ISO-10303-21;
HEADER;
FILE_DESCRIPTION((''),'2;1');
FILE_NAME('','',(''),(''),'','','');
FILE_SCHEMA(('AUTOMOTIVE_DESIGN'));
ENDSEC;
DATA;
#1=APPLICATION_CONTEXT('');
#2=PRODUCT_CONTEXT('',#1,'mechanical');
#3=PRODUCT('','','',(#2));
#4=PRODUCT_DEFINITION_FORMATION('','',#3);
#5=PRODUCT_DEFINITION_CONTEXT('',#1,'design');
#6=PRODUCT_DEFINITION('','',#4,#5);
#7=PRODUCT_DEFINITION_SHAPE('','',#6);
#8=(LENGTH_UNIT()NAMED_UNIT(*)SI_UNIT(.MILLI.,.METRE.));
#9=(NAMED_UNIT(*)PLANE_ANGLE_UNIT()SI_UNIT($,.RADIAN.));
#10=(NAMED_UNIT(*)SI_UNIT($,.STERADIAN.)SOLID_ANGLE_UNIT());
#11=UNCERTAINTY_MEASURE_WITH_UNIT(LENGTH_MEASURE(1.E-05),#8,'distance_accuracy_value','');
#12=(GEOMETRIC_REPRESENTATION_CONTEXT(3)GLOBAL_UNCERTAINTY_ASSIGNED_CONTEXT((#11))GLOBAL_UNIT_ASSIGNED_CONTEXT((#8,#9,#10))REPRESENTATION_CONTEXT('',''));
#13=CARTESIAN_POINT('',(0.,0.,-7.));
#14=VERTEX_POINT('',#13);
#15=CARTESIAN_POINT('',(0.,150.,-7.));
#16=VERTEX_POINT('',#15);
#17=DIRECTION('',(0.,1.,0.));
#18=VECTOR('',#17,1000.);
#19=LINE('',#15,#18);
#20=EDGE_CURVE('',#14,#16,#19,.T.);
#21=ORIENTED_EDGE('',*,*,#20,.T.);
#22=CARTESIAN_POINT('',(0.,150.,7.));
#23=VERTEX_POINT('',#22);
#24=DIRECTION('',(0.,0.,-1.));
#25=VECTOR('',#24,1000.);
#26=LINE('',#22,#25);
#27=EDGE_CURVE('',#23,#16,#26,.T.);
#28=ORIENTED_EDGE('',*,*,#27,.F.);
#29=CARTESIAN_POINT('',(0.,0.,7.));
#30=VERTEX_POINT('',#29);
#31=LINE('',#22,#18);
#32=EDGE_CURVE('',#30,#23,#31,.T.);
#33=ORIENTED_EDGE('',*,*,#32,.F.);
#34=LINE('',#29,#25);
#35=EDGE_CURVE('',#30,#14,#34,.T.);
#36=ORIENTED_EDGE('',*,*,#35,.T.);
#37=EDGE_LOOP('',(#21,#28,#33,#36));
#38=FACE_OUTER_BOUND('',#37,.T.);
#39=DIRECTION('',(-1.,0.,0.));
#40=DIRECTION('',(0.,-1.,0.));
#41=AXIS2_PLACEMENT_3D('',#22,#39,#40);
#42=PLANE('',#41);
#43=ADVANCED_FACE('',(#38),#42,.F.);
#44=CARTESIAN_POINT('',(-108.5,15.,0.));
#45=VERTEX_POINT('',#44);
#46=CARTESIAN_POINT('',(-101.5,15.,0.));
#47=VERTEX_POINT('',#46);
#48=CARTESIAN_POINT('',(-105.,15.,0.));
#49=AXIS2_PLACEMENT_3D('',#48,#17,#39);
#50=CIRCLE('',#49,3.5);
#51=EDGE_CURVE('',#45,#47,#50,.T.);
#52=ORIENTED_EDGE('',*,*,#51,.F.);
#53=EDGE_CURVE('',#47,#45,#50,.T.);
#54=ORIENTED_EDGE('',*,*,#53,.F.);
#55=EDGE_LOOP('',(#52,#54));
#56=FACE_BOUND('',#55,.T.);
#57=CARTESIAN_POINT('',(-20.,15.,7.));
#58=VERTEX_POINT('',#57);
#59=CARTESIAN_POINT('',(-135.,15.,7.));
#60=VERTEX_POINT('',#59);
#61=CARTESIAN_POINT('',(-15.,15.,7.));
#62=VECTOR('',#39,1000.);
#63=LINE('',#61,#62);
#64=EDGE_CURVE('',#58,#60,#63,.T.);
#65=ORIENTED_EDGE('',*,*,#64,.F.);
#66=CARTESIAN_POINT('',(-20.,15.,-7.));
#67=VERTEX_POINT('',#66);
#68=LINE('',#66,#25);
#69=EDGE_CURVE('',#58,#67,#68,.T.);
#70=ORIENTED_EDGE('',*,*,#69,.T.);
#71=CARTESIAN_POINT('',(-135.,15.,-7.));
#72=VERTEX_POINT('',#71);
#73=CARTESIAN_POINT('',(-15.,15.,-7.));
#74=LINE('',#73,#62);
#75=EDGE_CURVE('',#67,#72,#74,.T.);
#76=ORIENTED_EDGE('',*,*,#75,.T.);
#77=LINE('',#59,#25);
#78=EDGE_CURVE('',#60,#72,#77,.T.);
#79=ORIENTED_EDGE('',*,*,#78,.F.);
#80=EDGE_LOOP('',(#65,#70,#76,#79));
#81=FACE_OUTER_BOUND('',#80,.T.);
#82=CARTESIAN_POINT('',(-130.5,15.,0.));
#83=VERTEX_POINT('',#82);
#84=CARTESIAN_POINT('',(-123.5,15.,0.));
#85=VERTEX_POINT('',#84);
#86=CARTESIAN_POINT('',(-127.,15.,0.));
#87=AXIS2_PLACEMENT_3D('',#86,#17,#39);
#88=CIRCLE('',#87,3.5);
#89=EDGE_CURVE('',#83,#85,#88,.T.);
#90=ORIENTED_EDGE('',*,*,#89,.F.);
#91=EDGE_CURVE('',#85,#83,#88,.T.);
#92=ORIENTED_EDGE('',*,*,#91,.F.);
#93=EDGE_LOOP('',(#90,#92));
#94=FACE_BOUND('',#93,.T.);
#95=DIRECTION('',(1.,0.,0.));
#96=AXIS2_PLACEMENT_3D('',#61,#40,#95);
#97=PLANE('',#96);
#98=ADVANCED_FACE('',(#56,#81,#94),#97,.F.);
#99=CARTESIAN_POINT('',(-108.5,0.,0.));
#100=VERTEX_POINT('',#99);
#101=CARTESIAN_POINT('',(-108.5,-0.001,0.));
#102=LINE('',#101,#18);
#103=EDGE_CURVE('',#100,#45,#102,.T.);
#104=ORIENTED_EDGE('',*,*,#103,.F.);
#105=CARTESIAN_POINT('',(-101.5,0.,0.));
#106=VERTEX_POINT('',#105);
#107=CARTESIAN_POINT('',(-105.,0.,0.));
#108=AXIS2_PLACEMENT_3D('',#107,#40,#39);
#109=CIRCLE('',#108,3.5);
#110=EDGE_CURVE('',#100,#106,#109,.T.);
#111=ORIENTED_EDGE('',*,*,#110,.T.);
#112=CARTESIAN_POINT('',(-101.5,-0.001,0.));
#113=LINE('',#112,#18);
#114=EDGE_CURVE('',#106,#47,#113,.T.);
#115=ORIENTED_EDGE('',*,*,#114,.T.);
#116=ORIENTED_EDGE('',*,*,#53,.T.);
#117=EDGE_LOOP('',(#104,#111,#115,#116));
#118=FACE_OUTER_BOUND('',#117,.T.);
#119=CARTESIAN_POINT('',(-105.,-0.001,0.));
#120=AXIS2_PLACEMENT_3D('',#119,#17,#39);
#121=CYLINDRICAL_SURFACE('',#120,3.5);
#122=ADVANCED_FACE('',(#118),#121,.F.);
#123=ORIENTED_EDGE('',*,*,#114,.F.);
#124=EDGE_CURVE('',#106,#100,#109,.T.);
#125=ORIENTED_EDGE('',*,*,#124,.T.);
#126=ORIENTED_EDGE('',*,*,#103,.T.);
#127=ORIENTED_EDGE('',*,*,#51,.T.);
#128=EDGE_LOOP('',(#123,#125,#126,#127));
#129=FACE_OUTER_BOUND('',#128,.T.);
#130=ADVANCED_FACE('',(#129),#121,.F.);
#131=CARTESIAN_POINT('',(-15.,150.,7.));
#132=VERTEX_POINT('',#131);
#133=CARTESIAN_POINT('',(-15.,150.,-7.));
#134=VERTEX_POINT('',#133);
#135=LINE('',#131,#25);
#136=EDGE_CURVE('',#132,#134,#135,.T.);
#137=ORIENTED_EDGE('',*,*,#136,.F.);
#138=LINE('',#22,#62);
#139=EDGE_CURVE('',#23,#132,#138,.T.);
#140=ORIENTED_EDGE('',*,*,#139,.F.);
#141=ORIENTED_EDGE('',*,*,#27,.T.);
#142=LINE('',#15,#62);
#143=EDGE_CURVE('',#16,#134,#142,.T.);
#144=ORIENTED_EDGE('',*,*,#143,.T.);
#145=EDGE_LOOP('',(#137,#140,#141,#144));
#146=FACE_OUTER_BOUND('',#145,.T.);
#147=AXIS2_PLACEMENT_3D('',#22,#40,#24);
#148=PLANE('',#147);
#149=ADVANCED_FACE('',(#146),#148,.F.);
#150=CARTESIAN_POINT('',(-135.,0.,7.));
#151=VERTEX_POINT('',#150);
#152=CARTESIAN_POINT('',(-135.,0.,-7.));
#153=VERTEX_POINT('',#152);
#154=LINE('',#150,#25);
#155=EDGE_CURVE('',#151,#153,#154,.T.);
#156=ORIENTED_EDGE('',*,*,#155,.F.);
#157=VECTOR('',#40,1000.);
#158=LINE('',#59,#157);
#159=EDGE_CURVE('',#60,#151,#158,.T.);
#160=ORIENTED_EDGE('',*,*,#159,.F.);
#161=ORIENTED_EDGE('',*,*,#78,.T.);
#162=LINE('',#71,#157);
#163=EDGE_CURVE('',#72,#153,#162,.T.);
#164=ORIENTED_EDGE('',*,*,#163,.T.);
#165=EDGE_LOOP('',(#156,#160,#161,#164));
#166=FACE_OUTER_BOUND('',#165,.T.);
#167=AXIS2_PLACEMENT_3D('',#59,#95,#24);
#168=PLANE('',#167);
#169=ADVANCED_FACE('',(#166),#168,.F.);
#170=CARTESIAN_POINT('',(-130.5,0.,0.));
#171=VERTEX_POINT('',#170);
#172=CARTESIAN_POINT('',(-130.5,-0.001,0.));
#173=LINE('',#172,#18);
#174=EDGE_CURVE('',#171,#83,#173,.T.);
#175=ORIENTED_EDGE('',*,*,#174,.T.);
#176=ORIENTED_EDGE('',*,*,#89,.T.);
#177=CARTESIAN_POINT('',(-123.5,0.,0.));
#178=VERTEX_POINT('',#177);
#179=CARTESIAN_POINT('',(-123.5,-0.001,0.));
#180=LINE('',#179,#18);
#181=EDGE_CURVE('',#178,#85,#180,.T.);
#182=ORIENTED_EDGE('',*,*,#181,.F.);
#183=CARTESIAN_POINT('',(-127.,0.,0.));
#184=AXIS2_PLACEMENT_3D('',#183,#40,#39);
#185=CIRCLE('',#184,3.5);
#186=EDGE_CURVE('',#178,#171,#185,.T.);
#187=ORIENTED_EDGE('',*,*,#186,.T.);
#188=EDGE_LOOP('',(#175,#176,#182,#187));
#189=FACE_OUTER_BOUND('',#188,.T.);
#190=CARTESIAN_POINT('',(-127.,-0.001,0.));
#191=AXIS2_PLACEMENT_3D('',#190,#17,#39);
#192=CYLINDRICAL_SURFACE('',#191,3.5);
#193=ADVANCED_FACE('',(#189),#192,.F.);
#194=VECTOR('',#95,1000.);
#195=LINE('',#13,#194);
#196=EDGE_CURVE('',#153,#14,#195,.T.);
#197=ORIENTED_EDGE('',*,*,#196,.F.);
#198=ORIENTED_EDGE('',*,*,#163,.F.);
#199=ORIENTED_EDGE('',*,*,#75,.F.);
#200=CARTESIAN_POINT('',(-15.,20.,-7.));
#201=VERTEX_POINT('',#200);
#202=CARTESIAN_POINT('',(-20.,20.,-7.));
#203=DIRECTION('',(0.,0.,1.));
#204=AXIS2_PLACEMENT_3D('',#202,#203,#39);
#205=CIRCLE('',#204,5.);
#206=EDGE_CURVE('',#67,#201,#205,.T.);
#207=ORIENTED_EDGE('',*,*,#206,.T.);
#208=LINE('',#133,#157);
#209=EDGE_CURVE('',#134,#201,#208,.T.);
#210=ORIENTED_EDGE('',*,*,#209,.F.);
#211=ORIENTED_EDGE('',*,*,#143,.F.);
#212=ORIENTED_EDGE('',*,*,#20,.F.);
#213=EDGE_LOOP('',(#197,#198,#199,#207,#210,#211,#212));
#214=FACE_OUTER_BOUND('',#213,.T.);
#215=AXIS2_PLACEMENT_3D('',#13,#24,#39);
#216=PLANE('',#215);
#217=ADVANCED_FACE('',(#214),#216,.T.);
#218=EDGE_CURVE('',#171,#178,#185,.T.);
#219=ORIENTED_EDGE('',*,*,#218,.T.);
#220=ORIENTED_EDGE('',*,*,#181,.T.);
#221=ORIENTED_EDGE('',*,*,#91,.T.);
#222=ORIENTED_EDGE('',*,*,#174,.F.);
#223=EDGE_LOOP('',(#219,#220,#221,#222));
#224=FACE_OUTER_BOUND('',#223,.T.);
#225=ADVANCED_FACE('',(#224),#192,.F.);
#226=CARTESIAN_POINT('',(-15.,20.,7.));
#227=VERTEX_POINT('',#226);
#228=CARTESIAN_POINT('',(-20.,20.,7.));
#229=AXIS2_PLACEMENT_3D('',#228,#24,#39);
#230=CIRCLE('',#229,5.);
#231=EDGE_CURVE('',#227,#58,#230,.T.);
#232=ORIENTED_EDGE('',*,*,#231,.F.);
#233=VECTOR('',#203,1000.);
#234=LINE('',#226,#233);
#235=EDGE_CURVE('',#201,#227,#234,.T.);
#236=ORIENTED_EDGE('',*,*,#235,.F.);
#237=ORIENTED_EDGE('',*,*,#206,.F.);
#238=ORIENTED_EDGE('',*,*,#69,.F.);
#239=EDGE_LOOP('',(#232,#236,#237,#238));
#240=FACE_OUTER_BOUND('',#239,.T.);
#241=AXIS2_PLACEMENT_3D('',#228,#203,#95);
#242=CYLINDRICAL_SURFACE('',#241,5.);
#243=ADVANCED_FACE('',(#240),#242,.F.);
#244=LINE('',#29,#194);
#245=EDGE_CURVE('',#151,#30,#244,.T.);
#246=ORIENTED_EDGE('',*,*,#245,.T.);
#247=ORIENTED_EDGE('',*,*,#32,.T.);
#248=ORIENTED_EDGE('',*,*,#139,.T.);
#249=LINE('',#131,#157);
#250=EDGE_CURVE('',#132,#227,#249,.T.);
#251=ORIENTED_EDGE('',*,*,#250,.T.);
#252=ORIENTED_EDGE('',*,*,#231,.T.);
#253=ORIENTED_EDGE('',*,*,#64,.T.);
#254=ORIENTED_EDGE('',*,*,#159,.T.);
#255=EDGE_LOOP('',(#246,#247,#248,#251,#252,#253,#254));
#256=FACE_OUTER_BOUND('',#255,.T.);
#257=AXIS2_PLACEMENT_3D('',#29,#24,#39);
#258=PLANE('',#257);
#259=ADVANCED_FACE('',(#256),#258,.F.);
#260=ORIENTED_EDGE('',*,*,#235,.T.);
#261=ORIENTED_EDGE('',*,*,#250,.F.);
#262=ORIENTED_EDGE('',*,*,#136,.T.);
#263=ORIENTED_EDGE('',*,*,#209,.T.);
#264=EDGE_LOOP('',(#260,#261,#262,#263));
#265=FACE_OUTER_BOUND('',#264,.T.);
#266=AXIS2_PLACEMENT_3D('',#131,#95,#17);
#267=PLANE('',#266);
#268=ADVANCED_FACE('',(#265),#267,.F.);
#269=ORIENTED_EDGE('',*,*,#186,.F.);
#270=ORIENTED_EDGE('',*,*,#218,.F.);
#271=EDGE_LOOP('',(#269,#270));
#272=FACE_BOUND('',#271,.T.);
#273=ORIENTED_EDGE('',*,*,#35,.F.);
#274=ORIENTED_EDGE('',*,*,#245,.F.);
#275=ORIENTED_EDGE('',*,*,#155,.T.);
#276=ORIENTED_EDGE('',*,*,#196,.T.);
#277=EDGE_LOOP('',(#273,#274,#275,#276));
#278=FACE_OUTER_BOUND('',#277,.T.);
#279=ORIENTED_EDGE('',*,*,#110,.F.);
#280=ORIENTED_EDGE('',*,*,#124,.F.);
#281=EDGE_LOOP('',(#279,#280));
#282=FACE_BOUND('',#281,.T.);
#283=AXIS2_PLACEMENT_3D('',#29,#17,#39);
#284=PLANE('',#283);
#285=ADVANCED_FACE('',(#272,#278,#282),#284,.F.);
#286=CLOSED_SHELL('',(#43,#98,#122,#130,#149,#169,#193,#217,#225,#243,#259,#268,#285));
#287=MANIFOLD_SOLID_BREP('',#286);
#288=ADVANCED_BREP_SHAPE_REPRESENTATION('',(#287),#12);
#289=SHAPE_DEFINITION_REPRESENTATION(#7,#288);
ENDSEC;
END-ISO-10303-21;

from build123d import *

# Parameters (mm, degrees)
EXTRUDE_1_DEPTH     = 7
FILLET_1_R          = 5
CUT_EXTRUDE_1_REACH = 193.047
SKETCH_3_R          = 3.5


with BuildPart() as part:
    # 草图1 → 凸台-拉伸1 (new, symmetric)
    with BuildSketch(Plane.XY):
        Polygon((0, 150), (-15, 150), (-15, 15), (-135, 15), (-135, 0), (0, 0), align=None)
    extrude(amount=EXTRUDE_1_DEPTH, both=True)

    # 圆角1
    fillet_1_edges = [part.edges().sort_by_distance(p)[0] for p in [
        (-15, 15, 0),
    ]]
    fillet(fillet_1_edges, radius=FILLET_1_R)

    # 草图3 → 切除-拉伸1 (cut, up to next)
    with BuildSketch(Plane(origin=(0, 15, 0), x_dir=(1, 0, 0), z_dir=(0, 1, 0)), mode=Mode.PRIVATE) as cut_extrude_1_sk1:
        with Locations(Location((-127, 0, 0), (0, 0, 180))):
            Circle(SKETCH_3_R)
    cut_extrude_1_tool1 = extrude(cut_extrude_1_sk1.sketch, amount=-CUT_EXTRUDE_1_REACH, mode=Mode.PRIVATE) & part.part
    # 草图3 → 切除-拉伸1 (cut, up to next)
    with BuildSketch(Plane(origin=(0, 15, 0), x_dir=(1, 0, 0), z_dir=(0, 1, 0)), mode=Mode.PRIVATE) as cut_extrude_1_sk2:
        with Locations(Location((-105, 0, 0), (0, 0, 180))):
            Circle(SKETCH_3_R)
    cut_extrude_1_tool2 = extrude(cut_extrude_1_sk2.sketch, amount=-CUT_EXTRUDE_1_REACH, mode=Mode.PRIVATE) & part.part
    add(cut_extrude_1_tool1.solids().sort_by_distance((-127, 15, 0))[0], mode=Mode.SUBTRACT)
    add(cut_extrude_1_tool2.solids().sort_by_distance((-105, 15, 0))[0], mode=Mode.SUBTRACT)


solid = part.part
